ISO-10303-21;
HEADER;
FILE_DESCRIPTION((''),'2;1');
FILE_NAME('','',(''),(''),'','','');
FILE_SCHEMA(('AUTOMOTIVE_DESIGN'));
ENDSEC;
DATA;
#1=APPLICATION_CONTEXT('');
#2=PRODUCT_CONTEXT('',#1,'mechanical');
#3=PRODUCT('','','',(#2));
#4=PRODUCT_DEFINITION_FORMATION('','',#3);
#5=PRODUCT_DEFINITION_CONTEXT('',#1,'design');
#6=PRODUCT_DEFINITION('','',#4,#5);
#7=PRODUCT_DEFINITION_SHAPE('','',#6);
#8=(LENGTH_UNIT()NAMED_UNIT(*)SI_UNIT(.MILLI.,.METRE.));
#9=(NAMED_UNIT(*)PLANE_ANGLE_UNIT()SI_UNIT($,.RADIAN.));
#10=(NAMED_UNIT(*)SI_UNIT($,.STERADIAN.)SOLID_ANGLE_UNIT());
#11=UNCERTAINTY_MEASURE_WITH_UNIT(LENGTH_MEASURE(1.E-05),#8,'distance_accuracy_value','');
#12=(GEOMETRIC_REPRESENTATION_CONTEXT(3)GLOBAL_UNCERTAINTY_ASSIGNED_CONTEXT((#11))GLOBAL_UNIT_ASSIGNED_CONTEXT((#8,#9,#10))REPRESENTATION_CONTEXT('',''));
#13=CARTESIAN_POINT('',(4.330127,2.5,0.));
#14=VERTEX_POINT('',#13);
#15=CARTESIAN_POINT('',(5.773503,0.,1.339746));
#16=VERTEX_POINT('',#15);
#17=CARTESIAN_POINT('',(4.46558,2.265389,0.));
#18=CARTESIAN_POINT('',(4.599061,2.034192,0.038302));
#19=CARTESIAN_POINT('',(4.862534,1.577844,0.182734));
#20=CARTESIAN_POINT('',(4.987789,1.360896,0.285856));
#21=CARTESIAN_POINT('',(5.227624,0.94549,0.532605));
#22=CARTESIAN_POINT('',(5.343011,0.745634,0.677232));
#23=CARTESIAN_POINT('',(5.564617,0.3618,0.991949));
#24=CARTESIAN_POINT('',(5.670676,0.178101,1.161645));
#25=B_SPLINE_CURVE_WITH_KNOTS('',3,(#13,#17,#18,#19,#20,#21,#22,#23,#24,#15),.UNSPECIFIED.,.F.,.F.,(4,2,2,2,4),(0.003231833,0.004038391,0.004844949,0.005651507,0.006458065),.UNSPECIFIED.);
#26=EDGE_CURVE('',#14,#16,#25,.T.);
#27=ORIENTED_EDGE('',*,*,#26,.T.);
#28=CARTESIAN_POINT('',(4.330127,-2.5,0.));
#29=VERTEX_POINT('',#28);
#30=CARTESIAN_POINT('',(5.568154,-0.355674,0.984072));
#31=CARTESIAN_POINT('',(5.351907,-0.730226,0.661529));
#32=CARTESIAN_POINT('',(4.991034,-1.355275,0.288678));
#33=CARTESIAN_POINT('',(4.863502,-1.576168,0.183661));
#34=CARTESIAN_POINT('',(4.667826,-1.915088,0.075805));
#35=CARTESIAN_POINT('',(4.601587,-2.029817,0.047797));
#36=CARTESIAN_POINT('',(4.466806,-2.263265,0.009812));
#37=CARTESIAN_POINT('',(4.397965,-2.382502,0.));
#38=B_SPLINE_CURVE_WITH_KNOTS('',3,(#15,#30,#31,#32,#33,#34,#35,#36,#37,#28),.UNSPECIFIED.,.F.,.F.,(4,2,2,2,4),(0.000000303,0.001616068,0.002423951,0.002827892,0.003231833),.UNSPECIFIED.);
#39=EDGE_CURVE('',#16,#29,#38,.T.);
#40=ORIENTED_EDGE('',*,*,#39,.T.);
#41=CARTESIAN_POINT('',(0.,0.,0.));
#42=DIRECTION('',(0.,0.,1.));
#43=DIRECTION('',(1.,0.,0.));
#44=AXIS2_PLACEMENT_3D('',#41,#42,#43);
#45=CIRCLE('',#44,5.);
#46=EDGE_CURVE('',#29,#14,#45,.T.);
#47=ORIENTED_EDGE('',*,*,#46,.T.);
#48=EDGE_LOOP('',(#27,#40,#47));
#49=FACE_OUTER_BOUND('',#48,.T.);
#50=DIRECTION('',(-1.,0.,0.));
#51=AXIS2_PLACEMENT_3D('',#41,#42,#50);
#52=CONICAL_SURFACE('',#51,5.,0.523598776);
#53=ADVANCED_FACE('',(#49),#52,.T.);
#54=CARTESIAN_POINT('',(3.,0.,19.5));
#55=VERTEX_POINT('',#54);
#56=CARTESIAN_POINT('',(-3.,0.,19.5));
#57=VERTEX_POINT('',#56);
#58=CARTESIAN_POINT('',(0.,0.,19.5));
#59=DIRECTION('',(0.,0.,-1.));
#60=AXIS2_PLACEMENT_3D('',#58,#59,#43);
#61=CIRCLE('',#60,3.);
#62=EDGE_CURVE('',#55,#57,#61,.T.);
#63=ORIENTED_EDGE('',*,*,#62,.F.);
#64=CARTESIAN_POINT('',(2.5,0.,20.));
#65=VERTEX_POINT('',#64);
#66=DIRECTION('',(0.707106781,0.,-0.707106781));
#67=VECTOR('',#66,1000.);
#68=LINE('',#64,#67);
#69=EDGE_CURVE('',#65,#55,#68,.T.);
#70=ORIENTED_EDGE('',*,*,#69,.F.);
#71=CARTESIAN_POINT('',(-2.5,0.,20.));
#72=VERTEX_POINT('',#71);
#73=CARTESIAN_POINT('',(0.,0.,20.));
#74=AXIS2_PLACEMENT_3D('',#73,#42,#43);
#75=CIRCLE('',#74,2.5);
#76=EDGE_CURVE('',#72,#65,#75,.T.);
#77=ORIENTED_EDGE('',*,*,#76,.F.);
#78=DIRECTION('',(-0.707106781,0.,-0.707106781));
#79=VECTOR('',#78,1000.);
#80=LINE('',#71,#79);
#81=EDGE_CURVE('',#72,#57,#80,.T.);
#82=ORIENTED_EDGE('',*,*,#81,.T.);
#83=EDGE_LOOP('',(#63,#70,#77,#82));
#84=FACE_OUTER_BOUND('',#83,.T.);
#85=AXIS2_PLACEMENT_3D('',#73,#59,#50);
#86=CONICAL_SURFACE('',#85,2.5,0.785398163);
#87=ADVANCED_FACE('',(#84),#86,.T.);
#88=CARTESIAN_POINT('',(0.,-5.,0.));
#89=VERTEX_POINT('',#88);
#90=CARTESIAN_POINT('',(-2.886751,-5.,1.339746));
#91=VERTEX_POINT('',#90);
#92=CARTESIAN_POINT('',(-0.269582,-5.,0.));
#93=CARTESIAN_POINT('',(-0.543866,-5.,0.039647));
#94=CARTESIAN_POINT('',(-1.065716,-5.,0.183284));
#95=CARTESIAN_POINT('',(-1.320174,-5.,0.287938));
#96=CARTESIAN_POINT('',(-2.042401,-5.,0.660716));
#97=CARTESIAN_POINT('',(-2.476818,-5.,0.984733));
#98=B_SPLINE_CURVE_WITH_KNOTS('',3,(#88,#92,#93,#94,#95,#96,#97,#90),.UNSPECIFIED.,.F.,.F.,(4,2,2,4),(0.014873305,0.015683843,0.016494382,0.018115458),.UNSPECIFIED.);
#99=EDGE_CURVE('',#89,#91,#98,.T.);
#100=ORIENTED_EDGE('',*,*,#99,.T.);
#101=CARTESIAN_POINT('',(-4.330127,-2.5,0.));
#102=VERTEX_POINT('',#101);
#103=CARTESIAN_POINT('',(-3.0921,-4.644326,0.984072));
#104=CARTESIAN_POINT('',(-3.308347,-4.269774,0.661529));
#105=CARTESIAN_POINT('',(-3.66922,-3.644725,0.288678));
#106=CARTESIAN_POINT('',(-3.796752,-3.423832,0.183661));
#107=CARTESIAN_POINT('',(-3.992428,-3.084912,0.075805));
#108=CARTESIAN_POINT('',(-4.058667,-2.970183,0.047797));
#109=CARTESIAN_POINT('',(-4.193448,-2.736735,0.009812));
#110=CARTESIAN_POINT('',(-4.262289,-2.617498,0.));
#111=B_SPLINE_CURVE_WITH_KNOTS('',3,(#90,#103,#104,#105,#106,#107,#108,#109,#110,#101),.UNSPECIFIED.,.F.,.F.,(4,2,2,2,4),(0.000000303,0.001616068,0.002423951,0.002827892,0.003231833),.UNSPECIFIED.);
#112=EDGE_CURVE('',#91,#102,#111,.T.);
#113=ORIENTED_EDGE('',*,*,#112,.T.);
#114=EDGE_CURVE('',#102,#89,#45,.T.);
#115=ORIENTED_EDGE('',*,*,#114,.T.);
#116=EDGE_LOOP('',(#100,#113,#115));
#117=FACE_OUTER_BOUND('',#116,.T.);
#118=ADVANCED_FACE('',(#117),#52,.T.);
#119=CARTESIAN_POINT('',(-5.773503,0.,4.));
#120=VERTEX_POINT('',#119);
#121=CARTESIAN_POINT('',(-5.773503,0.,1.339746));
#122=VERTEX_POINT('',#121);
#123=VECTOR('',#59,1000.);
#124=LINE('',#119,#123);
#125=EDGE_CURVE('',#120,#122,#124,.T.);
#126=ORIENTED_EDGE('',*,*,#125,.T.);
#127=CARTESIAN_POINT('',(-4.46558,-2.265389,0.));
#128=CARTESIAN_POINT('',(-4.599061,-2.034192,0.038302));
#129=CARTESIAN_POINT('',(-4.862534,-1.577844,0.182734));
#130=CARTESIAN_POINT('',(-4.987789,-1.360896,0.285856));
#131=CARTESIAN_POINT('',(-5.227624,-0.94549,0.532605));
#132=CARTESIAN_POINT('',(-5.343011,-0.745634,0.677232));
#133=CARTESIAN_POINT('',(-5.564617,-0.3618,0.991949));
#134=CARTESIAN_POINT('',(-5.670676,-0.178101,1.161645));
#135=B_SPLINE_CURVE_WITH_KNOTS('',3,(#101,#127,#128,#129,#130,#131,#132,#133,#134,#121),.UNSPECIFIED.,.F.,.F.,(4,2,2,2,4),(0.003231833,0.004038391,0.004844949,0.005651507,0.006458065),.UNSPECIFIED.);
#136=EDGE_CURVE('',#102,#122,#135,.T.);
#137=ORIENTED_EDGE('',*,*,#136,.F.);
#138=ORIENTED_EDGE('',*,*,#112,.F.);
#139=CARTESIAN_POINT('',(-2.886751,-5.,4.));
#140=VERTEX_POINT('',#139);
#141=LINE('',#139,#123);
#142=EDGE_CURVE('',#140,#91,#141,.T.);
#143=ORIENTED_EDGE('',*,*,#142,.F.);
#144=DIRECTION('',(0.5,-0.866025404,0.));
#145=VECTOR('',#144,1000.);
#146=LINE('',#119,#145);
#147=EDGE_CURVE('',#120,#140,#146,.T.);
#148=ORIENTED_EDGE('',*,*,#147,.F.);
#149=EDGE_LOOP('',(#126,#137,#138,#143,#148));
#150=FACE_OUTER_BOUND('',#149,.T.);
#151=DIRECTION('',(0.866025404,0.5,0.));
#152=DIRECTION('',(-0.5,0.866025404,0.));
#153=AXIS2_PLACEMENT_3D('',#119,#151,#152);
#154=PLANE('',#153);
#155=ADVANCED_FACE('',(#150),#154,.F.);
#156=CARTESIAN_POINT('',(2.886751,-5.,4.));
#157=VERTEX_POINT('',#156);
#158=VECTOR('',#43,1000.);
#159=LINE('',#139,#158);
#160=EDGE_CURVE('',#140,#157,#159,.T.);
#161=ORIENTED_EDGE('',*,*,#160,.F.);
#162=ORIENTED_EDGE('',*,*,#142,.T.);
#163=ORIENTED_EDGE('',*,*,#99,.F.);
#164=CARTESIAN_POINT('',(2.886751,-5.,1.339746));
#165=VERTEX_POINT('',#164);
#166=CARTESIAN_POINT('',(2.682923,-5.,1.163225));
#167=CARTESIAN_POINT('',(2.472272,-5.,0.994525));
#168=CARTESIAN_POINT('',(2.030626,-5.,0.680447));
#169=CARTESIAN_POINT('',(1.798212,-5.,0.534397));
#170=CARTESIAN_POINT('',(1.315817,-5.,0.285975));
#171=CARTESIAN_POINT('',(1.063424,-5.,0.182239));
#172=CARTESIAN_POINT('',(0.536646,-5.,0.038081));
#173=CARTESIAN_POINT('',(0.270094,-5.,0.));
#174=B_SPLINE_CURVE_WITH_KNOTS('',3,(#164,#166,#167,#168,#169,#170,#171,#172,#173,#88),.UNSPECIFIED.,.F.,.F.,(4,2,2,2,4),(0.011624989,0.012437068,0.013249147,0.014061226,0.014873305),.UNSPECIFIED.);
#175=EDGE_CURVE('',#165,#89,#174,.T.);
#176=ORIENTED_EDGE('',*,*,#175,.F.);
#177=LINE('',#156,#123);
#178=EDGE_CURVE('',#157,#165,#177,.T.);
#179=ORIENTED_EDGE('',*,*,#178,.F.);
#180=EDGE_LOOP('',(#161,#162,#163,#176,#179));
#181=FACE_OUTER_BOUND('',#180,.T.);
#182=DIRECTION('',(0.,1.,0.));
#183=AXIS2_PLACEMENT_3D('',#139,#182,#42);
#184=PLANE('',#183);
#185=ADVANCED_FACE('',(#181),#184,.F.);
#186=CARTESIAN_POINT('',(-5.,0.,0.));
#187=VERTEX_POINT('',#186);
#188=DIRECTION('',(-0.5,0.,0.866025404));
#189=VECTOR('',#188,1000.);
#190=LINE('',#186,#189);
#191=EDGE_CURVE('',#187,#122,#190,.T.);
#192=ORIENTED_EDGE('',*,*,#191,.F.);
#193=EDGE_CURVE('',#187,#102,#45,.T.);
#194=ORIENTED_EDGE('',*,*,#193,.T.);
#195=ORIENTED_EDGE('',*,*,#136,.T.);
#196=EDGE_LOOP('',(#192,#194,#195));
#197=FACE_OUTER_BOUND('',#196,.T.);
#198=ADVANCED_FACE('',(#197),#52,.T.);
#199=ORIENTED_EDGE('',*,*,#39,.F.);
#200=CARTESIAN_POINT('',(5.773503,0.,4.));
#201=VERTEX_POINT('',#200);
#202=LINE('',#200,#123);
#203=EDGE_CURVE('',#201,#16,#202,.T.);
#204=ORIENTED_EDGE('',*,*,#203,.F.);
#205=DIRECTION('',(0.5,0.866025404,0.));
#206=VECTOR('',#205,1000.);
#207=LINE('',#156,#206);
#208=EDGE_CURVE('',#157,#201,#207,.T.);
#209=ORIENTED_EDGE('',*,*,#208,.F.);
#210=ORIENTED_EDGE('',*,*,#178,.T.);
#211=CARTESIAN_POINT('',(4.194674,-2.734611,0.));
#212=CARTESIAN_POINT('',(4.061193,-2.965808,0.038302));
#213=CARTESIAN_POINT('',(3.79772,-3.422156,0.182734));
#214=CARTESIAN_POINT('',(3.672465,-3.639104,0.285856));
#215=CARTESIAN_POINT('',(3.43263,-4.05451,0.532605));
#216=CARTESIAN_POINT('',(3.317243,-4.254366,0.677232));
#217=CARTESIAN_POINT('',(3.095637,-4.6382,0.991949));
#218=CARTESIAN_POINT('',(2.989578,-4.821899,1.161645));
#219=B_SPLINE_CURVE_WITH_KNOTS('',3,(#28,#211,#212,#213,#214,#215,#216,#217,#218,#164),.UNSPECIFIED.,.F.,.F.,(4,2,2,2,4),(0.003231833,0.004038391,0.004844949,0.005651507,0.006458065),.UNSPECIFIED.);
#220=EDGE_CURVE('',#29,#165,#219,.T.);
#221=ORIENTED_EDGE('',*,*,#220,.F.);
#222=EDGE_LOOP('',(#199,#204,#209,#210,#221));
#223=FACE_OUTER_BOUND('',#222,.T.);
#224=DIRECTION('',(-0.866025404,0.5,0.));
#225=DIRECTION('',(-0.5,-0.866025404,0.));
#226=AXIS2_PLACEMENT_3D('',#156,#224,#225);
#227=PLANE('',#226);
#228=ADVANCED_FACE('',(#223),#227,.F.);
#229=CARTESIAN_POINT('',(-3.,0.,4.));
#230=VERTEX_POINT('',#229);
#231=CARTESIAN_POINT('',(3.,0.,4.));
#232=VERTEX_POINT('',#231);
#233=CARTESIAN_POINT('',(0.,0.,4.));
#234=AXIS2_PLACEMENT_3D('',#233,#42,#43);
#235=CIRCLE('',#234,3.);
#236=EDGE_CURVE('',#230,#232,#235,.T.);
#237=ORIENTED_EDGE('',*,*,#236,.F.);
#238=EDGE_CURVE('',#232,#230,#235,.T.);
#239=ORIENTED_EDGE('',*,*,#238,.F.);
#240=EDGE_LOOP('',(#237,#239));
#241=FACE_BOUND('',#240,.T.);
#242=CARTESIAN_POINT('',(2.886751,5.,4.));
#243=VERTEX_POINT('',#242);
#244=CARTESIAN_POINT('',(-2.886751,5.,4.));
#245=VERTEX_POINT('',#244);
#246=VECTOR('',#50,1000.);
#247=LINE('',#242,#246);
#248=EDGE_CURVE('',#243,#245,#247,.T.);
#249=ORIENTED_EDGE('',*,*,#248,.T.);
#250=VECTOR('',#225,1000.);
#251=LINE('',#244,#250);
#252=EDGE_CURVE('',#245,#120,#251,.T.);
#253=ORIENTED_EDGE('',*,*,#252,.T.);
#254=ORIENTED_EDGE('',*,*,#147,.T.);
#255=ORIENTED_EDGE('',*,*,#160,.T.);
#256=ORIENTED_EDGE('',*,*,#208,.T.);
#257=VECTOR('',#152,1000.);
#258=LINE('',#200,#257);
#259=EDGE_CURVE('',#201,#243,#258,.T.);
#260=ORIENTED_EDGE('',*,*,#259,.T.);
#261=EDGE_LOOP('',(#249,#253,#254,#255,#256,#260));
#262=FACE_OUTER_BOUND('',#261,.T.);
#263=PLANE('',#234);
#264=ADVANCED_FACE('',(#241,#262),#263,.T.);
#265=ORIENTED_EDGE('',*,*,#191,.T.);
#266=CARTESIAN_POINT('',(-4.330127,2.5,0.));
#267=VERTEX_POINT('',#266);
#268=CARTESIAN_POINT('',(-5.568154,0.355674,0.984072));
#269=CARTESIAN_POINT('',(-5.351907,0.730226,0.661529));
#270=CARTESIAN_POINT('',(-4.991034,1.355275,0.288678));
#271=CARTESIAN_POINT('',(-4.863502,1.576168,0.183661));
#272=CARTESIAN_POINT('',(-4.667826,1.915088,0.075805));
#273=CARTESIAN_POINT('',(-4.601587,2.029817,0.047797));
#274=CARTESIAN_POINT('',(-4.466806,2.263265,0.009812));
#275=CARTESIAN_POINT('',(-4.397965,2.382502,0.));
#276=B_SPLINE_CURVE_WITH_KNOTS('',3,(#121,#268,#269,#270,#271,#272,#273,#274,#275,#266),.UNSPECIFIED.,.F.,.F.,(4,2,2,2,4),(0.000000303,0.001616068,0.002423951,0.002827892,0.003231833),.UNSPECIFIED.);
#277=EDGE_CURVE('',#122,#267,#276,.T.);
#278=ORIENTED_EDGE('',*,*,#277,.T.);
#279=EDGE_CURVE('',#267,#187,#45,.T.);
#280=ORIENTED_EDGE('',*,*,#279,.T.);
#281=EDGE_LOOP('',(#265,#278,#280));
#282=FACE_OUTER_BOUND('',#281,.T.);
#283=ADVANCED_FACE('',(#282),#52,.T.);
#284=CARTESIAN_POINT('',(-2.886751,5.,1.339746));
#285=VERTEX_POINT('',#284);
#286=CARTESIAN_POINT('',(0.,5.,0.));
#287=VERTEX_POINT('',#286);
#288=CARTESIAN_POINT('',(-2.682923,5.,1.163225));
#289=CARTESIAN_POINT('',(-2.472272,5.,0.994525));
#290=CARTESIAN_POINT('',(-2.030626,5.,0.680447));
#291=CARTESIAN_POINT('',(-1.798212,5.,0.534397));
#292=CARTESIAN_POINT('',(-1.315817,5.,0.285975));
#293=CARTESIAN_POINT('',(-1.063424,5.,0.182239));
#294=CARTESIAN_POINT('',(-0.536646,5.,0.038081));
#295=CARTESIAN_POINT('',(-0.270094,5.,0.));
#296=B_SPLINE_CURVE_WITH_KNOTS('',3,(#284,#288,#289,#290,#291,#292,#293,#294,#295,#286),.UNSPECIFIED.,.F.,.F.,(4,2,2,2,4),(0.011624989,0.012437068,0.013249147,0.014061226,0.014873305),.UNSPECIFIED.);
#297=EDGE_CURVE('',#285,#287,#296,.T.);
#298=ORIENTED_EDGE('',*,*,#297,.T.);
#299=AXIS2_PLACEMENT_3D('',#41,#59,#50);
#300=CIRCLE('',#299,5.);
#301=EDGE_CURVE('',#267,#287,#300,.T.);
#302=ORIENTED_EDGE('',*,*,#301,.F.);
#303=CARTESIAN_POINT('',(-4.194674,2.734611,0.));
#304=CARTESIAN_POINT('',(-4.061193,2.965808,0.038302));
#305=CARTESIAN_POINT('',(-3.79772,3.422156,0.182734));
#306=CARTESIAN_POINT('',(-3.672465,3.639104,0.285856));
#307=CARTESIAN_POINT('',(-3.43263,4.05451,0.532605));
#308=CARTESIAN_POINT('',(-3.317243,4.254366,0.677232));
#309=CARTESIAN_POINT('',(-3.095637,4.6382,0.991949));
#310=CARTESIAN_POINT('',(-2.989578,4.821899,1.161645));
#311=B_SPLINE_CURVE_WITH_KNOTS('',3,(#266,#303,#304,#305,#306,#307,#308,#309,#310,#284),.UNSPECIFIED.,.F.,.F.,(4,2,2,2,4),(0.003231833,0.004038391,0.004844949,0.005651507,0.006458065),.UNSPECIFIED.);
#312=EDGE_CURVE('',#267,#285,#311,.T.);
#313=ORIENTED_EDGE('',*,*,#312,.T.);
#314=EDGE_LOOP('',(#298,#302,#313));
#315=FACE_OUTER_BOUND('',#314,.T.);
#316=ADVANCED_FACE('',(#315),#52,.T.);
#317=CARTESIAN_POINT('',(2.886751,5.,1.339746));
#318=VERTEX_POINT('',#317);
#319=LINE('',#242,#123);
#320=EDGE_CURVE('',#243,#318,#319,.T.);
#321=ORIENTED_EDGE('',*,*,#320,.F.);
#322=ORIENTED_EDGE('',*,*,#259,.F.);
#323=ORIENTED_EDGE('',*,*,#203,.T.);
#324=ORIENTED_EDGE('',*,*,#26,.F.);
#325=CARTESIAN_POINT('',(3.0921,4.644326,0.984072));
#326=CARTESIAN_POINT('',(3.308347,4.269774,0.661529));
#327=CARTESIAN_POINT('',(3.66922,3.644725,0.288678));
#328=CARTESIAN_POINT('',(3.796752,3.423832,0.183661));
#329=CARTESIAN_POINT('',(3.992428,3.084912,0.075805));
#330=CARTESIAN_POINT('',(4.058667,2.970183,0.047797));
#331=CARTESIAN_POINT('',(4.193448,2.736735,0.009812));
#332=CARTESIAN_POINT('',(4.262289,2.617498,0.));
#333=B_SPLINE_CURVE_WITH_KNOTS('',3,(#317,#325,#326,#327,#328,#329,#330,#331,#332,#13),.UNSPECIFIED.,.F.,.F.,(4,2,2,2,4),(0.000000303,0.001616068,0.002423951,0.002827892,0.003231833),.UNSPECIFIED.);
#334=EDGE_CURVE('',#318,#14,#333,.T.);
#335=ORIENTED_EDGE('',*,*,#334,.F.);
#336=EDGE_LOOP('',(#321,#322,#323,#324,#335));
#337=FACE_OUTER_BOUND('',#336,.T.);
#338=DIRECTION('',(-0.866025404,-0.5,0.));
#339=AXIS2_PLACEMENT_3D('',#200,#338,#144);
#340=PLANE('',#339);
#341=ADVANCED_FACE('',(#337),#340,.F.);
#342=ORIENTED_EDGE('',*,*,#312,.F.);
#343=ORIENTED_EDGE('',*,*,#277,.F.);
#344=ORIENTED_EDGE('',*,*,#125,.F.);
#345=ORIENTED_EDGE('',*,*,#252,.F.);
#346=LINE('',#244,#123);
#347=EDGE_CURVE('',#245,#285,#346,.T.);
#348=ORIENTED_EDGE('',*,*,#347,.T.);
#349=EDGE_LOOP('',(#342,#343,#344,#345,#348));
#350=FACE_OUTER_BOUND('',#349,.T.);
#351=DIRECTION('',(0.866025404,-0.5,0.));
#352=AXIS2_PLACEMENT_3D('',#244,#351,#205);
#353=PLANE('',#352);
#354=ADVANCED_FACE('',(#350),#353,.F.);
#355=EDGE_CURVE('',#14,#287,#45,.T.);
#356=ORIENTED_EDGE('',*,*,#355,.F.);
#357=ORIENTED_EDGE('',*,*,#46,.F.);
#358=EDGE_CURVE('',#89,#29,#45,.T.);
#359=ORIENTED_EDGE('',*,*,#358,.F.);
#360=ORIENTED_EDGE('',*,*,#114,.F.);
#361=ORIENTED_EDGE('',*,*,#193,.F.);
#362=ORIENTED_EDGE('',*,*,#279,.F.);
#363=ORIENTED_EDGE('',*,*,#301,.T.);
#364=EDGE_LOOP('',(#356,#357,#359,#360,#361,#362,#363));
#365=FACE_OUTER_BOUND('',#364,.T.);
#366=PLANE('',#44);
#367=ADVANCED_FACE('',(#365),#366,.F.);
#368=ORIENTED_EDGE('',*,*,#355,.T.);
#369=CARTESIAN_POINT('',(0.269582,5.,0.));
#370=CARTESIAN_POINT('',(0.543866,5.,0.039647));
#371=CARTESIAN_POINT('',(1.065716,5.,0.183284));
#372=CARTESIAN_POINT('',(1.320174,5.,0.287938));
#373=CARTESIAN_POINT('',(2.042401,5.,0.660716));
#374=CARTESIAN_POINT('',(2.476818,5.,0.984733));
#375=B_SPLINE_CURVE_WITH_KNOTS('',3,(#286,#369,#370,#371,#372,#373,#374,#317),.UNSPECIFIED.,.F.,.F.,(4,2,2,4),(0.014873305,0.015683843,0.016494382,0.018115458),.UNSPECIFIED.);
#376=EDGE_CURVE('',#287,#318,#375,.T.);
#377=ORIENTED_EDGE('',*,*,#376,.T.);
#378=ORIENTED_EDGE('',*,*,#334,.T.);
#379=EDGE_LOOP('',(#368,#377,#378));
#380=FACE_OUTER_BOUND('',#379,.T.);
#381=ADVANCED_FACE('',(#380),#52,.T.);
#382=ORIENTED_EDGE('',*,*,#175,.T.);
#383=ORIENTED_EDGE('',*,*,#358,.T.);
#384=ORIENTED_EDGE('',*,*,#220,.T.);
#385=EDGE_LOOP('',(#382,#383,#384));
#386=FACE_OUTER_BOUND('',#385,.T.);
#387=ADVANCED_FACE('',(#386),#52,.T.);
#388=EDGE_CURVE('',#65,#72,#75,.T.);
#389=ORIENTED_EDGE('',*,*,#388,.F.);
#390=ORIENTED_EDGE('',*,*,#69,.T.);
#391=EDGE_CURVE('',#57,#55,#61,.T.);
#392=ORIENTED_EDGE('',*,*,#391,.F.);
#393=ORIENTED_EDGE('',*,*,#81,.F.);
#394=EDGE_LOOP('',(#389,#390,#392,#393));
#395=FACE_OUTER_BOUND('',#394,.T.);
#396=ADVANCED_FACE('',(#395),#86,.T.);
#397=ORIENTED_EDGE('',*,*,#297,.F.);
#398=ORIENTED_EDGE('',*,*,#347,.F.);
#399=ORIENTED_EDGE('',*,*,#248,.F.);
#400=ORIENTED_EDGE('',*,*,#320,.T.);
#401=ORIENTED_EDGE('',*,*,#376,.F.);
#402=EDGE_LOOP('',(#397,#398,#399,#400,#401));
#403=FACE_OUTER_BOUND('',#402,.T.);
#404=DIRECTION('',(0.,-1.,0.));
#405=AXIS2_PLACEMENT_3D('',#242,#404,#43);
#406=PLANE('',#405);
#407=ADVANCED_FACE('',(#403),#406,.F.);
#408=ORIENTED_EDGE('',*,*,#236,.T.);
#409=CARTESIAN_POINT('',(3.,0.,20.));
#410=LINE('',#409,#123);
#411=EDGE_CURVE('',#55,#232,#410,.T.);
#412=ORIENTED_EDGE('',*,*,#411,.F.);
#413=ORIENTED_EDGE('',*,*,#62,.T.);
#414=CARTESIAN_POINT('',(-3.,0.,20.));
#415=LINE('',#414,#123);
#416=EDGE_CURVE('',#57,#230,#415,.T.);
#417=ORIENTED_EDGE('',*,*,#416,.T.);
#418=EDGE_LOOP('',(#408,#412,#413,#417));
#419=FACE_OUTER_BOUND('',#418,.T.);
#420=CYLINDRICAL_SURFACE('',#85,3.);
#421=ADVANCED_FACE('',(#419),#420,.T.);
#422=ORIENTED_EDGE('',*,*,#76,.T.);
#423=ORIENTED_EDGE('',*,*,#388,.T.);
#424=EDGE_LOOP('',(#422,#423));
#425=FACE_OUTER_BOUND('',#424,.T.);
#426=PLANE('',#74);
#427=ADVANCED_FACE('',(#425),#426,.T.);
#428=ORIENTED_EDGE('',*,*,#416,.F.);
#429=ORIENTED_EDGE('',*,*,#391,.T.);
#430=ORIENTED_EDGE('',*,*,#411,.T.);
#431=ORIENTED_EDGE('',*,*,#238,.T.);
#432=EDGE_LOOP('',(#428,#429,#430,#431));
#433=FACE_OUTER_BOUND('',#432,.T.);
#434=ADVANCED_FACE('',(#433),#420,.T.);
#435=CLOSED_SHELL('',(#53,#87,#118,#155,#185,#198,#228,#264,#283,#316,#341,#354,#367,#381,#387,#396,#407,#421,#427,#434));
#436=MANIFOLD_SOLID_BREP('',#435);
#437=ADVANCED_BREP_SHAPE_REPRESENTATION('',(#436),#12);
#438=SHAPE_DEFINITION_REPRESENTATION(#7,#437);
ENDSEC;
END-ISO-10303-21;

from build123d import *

# Parameters (mm, degrees)
BOSS_EXTRUDE1_DEPTH = 4
SKETCH2_OUTSIDE_W   = 21.324
SKETCH2_OUTSIDE_H   = 19.776
SKETCH2_OUTSIDE_R   = 5
CUT_EXTRUDE1_DEPTH  = 4
CUT_EXTRUDE1_DRAFT  = -30
SKETCH3_R           = 3
BOSS_EXTRUDE2_DEPTH = 16
CHAMFER1_SIZE       = 0.5


with BuildPart() as part:
    # Sketch1 → Boss-Extrude1 (new body)
    with BuildSketch(Plane.XY):
        Polygon((2.886751346, 5), (-2.886751346, 5), (-5.773502692, 0), (-2.886751346, -5), (2.886751346, -5), (5.773502692, 0), align=None)
    extrude(amount=BOSS_EXTRUDE1_DEPTH)


with BuildPart() as cut_extrude1_tool:
    # Sketch2 outside → Cut-Extrude1 (with draft: the straight prism first)
    with BuildSketch(Plane(origin=(0, 0, 0), x_dir=(-1, 0, 0), z_dir=(0, 0, -1))):
        Rectangle(SKETCH2_OUTSIDE_W, SKETCH2_OUTSIDE_H)
        Circle(SKETCH2_OUTSIDE_R, mode=Mode.SUBTRACT)
    extrude(amount=-CUT_EXTRUDE1_DEPTH)
    # Cut-Extrude1: the draft: its side faces are tilted about the plane it starts from
    cut_extrude1_sides = [cut_extrude1_tool.faces().sort_by_distance(p)[0] for p in [
        (0, -9.888, 2),
        (-10.662, 0, 2),
        (0, 9.888, 2),
        (10.662, 0, 2),
        (5, 0, 2),
    ]]
    draft(cut_extrude1_sides, Plane(origin=(0, 0, 0), x_dir=(-1, 0, 0), z_dir=(0, 0, -1)), CUT_EXTRUDE1_DRAFT)


with BuildPart() as part_1:
    add(part.part)

    # Cut-Extrude1: cut by cut_extrude1_tool
    add(cut_extrude1_tool.part, mode=Mode.SUBTRACT)

    # Sketch3 → Boss-Extrude2 (add)
    with BuildSketch(Plane.XY.offset(4)):
        Circle(SKETCH3_R)
    extrude(amount=BOSS_EXTRUDE2_DEPTH)

    # Chamfer1
    chamfer1_edges = [part_1.edges().sort_by_distance(p)[0] for p in [
        (-3, 0, 20),
    ]]
    chamfer(chamfer1_edges, length=CHAMFER1_SIZE)


solid = part_1.part
